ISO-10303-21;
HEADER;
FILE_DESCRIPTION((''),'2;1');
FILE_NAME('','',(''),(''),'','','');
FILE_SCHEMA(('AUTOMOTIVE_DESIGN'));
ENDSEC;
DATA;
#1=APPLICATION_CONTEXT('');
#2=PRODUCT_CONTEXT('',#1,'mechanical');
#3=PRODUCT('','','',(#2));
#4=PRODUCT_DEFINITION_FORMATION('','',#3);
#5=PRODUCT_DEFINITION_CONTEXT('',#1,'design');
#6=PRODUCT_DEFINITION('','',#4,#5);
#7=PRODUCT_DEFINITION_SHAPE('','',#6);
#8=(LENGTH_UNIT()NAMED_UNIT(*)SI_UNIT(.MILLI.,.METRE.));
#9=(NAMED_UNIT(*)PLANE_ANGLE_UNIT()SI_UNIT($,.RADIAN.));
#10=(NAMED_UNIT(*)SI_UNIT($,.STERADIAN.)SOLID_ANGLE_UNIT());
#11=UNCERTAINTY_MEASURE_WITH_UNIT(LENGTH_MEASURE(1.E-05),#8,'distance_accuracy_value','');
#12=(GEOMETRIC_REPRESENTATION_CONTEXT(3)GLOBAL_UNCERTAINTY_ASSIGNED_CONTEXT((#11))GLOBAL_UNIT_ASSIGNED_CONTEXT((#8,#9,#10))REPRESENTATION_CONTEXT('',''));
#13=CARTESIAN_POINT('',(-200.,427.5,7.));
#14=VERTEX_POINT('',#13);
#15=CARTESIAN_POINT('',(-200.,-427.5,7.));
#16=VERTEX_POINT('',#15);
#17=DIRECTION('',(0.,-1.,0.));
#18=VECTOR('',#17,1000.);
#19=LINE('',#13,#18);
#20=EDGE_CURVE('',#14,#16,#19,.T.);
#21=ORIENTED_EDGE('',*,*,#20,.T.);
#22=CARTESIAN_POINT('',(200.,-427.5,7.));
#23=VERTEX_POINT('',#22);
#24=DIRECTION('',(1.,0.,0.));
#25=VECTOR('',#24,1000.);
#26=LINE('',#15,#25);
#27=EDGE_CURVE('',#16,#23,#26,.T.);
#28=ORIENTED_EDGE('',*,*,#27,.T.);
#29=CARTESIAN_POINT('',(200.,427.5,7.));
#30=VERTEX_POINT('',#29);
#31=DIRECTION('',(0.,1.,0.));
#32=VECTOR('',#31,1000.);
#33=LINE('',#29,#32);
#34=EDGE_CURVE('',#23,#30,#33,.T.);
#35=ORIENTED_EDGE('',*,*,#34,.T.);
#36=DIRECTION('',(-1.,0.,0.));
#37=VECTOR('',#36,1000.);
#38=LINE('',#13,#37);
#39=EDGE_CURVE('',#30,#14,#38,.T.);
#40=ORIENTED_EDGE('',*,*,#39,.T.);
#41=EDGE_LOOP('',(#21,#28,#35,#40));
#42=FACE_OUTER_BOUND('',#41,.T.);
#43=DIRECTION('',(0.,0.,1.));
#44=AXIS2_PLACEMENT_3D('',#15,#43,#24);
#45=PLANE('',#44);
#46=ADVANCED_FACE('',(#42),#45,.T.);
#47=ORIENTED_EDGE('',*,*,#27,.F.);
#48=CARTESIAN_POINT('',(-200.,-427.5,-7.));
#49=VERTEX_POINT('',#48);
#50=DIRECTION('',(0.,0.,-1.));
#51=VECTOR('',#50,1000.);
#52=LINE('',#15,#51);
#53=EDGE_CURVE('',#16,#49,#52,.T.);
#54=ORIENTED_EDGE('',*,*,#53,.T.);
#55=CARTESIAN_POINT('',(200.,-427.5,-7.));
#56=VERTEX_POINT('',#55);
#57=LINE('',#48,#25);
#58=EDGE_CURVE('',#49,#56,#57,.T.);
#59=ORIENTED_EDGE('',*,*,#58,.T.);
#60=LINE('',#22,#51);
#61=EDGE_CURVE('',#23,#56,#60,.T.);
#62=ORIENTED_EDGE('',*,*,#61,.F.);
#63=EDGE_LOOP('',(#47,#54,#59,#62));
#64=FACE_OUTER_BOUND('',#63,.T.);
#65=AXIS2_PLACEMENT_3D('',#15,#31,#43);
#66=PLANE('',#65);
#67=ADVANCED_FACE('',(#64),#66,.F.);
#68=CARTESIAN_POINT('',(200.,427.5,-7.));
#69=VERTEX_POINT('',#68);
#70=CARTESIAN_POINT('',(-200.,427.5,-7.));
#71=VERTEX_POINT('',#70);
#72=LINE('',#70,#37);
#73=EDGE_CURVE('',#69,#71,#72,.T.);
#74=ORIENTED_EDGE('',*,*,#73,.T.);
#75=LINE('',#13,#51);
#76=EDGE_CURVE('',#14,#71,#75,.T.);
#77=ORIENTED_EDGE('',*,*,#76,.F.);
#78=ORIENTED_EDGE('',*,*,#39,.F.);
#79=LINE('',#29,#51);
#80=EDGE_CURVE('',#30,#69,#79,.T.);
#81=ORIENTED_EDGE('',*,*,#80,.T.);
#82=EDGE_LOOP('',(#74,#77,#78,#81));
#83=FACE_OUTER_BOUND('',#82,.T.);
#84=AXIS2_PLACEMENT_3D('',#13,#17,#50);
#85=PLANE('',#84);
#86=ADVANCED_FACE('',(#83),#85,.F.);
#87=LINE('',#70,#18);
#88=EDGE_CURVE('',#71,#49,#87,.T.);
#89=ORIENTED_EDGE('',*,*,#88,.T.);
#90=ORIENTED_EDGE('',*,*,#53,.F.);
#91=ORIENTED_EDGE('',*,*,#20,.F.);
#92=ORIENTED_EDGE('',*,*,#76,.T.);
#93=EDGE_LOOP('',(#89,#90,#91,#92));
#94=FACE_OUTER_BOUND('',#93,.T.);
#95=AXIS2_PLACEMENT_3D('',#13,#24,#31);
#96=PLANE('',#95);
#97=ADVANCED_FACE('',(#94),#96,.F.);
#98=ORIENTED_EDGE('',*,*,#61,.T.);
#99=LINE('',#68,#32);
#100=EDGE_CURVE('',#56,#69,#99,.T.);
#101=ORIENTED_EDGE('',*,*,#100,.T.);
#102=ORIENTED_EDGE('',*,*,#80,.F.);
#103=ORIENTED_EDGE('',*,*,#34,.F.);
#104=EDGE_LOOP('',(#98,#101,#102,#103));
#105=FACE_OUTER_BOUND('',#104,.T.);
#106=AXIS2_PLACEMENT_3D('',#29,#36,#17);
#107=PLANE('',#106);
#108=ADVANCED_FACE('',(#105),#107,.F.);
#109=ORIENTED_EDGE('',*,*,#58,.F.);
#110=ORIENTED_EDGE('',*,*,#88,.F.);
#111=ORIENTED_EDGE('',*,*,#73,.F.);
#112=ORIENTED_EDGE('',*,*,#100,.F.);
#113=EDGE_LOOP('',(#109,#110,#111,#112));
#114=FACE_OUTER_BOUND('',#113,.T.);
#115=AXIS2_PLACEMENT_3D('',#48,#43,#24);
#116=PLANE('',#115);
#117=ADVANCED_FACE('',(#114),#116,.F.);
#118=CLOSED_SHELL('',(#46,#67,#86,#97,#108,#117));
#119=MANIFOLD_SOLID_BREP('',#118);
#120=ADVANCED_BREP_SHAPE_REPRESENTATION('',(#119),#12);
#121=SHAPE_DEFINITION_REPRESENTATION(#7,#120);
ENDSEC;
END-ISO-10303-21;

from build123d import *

# Parameters (mm, degrees)
SKETCH1_W           = 400
SKETCH1_H           = 855
BOSS_EXTRUDE1_DEPTH = 7


with BuildPart() as part:
    # Sketch1 → Boss-Extrude1 (new, symmetric)
    with BuildSketch(Plane.XY):
        Rectangle(SKETCH1_W, SKETCH1_H)
    extrude(amount=BOSS_EXTRUDE1_DEPTH, both=True)


solid = part.part
